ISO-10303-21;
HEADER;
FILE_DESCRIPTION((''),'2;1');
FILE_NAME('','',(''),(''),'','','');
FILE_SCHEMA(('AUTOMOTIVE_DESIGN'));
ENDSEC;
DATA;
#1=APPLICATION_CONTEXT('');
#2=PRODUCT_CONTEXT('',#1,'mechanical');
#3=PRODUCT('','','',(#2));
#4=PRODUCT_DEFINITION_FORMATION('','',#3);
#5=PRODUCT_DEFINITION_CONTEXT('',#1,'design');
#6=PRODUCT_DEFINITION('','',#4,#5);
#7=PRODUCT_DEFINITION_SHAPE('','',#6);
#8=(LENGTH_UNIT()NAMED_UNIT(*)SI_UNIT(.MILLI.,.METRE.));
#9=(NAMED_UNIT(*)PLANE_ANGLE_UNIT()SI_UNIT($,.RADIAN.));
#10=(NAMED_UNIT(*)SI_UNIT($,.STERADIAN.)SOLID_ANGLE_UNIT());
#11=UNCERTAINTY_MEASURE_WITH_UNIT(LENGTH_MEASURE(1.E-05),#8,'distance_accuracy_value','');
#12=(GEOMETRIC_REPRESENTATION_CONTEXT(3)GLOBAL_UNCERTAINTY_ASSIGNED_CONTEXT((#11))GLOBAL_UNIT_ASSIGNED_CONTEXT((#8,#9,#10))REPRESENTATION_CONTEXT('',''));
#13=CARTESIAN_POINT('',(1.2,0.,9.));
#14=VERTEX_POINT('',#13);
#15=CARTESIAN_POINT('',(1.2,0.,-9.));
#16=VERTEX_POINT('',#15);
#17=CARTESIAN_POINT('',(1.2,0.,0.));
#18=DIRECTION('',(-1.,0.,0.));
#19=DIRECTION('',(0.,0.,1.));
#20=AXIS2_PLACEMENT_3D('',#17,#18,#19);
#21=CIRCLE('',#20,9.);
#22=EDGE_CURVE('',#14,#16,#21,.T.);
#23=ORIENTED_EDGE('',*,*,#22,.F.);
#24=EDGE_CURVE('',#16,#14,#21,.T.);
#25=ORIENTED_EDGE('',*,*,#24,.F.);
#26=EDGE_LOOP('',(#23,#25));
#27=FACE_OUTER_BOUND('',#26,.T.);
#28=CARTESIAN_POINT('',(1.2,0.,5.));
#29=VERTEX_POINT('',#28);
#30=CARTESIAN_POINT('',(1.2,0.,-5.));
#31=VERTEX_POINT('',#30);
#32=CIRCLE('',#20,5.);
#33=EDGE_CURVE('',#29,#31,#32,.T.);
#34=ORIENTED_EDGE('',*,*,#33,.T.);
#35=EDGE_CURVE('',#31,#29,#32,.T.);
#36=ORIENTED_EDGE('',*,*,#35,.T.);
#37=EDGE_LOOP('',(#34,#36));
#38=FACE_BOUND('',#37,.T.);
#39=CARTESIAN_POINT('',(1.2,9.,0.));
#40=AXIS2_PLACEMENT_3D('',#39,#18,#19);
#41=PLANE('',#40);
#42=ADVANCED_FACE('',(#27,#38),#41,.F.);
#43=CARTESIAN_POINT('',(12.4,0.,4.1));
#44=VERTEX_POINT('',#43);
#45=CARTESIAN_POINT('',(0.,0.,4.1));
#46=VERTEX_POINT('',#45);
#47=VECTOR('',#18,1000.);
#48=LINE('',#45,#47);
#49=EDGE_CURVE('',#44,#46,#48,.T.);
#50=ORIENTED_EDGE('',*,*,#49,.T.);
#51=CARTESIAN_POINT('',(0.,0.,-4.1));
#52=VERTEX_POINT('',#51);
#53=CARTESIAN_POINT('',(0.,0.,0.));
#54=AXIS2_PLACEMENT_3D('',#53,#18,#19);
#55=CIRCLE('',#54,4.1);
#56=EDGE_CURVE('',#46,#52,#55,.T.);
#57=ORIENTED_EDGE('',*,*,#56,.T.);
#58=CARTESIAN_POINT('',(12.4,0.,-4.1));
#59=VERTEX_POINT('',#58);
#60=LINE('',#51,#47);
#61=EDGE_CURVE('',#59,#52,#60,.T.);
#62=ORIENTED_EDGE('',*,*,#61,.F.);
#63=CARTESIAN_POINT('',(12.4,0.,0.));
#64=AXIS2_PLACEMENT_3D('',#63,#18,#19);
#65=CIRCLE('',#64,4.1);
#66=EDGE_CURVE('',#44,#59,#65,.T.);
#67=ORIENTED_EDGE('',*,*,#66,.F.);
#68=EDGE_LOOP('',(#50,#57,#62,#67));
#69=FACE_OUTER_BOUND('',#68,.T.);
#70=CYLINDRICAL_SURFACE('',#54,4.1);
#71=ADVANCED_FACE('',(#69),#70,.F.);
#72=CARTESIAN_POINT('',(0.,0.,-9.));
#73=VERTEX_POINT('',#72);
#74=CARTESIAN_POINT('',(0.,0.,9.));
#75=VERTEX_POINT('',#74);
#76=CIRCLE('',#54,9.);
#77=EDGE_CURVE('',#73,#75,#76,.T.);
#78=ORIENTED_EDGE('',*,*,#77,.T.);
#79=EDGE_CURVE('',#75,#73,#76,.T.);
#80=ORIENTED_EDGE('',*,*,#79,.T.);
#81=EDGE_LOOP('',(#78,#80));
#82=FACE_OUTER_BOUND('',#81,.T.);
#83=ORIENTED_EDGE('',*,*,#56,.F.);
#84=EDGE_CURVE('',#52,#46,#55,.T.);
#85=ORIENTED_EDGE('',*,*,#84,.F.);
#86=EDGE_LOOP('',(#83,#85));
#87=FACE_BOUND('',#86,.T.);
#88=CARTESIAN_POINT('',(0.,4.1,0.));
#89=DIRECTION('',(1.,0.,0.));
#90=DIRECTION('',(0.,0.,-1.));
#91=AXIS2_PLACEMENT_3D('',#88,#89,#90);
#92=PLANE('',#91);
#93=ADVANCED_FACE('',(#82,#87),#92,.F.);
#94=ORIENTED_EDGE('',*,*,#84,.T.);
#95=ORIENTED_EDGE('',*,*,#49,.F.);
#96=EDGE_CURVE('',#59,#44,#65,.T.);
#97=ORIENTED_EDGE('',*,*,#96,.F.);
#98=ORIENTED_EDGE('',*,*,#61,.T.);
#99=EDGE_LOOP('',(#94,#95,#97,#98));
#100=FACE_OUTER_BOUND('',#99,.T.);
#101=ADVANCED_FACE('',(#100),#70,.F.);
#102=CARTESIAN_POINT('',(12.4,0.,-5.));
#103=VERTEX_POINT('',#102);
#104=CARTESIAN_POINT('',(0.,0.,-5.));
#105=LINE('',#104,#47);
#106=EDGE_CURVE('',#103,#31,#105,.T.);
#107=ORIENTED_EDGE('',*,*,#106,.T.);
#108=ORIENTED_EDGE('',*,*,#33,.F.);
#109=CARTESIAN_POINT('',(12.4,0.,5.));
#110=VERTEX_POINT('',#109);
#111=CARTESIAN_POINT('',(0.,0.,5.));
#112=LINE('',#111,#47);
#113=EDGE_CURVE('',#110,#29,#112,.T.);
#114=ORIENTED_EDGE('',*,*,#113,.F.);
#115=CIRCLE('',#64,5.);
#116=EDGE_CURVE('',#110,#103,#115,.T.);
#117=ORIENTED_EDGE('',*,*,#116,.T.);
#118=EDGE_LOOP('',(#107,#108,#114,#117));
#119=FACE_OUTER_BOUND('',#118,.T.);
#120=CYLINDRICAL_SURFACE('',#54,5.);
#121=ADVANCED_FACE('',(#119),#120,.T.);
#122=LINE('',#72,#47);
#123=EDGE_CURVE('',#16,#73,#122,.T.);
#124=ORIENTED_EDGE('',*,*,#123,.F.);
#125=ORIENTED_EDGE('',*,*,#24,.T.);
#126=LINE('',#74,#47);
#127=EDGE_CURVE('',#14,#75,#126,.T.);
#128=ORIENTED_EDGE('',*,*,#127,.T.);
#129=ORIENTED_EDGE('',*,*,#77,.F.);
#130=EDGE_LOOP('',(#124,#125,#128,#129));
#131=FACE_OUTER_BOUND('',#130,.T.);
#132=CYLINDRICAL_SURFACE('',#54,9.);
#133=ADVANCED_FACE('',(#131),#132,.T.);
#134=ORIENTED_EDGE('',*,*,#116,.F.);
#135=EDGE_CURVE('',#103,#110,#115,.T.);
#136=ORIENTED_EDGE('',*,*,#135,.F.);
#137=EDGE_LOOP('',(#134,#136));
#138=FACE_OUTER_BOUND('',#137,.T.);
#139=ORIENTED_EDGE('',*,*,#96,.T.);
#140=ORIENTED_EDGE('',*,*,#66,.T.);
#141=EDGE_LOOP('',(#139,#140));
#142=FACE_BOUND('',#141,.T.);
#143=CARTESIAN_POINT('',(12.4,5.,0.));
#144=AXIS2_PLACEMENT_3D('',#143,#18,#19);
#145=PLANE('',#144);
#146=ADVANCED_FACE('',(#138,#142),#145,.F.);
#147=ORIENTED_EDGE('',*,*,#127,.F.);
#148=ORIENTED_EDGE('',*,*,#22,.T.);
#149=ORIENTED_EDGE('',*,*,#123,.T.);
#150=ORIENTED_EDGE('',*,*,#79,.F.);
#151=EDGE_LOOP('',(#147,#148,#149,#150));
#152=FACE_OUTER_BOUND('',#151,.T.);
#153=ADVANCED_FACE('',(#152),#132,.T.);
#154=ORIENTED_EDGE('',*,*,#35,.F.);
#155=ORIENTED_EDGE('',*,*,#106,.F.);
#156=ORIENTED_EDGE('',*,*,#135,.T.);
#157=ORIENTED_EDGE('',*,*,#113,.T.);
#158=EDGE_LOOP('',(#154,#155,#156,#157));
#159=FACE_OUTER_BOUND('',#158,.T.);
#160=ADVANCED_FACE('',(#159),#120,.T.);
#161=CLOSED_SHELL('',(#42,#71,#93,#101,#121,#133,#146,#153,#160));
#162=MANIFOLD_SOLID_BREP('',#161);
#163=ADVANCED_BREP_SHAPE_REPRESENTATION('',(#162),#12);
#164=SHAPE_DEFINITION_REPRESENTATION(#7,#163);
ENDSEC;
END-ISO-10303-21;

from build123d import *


with BuildPart() as part:
    # 草图1 → 旋转1 (revolve)
    with BuildSketch(Plane.XY, mode=Mode.PRIVATE) as revolve_1_sk:
        Polygon((0, 4.1), (0, 9), (1.2, 9), (1.2, 5), (12.4, 5), (12.4, 4.1), align=None)
    revolve(revolve_1_sk.sketch.rotate(Axis((0, 0, 0), (1, 0, 0)), 90), axis=Axis((0, 0, 0), (1, 0, 0)))


solid = part.part
